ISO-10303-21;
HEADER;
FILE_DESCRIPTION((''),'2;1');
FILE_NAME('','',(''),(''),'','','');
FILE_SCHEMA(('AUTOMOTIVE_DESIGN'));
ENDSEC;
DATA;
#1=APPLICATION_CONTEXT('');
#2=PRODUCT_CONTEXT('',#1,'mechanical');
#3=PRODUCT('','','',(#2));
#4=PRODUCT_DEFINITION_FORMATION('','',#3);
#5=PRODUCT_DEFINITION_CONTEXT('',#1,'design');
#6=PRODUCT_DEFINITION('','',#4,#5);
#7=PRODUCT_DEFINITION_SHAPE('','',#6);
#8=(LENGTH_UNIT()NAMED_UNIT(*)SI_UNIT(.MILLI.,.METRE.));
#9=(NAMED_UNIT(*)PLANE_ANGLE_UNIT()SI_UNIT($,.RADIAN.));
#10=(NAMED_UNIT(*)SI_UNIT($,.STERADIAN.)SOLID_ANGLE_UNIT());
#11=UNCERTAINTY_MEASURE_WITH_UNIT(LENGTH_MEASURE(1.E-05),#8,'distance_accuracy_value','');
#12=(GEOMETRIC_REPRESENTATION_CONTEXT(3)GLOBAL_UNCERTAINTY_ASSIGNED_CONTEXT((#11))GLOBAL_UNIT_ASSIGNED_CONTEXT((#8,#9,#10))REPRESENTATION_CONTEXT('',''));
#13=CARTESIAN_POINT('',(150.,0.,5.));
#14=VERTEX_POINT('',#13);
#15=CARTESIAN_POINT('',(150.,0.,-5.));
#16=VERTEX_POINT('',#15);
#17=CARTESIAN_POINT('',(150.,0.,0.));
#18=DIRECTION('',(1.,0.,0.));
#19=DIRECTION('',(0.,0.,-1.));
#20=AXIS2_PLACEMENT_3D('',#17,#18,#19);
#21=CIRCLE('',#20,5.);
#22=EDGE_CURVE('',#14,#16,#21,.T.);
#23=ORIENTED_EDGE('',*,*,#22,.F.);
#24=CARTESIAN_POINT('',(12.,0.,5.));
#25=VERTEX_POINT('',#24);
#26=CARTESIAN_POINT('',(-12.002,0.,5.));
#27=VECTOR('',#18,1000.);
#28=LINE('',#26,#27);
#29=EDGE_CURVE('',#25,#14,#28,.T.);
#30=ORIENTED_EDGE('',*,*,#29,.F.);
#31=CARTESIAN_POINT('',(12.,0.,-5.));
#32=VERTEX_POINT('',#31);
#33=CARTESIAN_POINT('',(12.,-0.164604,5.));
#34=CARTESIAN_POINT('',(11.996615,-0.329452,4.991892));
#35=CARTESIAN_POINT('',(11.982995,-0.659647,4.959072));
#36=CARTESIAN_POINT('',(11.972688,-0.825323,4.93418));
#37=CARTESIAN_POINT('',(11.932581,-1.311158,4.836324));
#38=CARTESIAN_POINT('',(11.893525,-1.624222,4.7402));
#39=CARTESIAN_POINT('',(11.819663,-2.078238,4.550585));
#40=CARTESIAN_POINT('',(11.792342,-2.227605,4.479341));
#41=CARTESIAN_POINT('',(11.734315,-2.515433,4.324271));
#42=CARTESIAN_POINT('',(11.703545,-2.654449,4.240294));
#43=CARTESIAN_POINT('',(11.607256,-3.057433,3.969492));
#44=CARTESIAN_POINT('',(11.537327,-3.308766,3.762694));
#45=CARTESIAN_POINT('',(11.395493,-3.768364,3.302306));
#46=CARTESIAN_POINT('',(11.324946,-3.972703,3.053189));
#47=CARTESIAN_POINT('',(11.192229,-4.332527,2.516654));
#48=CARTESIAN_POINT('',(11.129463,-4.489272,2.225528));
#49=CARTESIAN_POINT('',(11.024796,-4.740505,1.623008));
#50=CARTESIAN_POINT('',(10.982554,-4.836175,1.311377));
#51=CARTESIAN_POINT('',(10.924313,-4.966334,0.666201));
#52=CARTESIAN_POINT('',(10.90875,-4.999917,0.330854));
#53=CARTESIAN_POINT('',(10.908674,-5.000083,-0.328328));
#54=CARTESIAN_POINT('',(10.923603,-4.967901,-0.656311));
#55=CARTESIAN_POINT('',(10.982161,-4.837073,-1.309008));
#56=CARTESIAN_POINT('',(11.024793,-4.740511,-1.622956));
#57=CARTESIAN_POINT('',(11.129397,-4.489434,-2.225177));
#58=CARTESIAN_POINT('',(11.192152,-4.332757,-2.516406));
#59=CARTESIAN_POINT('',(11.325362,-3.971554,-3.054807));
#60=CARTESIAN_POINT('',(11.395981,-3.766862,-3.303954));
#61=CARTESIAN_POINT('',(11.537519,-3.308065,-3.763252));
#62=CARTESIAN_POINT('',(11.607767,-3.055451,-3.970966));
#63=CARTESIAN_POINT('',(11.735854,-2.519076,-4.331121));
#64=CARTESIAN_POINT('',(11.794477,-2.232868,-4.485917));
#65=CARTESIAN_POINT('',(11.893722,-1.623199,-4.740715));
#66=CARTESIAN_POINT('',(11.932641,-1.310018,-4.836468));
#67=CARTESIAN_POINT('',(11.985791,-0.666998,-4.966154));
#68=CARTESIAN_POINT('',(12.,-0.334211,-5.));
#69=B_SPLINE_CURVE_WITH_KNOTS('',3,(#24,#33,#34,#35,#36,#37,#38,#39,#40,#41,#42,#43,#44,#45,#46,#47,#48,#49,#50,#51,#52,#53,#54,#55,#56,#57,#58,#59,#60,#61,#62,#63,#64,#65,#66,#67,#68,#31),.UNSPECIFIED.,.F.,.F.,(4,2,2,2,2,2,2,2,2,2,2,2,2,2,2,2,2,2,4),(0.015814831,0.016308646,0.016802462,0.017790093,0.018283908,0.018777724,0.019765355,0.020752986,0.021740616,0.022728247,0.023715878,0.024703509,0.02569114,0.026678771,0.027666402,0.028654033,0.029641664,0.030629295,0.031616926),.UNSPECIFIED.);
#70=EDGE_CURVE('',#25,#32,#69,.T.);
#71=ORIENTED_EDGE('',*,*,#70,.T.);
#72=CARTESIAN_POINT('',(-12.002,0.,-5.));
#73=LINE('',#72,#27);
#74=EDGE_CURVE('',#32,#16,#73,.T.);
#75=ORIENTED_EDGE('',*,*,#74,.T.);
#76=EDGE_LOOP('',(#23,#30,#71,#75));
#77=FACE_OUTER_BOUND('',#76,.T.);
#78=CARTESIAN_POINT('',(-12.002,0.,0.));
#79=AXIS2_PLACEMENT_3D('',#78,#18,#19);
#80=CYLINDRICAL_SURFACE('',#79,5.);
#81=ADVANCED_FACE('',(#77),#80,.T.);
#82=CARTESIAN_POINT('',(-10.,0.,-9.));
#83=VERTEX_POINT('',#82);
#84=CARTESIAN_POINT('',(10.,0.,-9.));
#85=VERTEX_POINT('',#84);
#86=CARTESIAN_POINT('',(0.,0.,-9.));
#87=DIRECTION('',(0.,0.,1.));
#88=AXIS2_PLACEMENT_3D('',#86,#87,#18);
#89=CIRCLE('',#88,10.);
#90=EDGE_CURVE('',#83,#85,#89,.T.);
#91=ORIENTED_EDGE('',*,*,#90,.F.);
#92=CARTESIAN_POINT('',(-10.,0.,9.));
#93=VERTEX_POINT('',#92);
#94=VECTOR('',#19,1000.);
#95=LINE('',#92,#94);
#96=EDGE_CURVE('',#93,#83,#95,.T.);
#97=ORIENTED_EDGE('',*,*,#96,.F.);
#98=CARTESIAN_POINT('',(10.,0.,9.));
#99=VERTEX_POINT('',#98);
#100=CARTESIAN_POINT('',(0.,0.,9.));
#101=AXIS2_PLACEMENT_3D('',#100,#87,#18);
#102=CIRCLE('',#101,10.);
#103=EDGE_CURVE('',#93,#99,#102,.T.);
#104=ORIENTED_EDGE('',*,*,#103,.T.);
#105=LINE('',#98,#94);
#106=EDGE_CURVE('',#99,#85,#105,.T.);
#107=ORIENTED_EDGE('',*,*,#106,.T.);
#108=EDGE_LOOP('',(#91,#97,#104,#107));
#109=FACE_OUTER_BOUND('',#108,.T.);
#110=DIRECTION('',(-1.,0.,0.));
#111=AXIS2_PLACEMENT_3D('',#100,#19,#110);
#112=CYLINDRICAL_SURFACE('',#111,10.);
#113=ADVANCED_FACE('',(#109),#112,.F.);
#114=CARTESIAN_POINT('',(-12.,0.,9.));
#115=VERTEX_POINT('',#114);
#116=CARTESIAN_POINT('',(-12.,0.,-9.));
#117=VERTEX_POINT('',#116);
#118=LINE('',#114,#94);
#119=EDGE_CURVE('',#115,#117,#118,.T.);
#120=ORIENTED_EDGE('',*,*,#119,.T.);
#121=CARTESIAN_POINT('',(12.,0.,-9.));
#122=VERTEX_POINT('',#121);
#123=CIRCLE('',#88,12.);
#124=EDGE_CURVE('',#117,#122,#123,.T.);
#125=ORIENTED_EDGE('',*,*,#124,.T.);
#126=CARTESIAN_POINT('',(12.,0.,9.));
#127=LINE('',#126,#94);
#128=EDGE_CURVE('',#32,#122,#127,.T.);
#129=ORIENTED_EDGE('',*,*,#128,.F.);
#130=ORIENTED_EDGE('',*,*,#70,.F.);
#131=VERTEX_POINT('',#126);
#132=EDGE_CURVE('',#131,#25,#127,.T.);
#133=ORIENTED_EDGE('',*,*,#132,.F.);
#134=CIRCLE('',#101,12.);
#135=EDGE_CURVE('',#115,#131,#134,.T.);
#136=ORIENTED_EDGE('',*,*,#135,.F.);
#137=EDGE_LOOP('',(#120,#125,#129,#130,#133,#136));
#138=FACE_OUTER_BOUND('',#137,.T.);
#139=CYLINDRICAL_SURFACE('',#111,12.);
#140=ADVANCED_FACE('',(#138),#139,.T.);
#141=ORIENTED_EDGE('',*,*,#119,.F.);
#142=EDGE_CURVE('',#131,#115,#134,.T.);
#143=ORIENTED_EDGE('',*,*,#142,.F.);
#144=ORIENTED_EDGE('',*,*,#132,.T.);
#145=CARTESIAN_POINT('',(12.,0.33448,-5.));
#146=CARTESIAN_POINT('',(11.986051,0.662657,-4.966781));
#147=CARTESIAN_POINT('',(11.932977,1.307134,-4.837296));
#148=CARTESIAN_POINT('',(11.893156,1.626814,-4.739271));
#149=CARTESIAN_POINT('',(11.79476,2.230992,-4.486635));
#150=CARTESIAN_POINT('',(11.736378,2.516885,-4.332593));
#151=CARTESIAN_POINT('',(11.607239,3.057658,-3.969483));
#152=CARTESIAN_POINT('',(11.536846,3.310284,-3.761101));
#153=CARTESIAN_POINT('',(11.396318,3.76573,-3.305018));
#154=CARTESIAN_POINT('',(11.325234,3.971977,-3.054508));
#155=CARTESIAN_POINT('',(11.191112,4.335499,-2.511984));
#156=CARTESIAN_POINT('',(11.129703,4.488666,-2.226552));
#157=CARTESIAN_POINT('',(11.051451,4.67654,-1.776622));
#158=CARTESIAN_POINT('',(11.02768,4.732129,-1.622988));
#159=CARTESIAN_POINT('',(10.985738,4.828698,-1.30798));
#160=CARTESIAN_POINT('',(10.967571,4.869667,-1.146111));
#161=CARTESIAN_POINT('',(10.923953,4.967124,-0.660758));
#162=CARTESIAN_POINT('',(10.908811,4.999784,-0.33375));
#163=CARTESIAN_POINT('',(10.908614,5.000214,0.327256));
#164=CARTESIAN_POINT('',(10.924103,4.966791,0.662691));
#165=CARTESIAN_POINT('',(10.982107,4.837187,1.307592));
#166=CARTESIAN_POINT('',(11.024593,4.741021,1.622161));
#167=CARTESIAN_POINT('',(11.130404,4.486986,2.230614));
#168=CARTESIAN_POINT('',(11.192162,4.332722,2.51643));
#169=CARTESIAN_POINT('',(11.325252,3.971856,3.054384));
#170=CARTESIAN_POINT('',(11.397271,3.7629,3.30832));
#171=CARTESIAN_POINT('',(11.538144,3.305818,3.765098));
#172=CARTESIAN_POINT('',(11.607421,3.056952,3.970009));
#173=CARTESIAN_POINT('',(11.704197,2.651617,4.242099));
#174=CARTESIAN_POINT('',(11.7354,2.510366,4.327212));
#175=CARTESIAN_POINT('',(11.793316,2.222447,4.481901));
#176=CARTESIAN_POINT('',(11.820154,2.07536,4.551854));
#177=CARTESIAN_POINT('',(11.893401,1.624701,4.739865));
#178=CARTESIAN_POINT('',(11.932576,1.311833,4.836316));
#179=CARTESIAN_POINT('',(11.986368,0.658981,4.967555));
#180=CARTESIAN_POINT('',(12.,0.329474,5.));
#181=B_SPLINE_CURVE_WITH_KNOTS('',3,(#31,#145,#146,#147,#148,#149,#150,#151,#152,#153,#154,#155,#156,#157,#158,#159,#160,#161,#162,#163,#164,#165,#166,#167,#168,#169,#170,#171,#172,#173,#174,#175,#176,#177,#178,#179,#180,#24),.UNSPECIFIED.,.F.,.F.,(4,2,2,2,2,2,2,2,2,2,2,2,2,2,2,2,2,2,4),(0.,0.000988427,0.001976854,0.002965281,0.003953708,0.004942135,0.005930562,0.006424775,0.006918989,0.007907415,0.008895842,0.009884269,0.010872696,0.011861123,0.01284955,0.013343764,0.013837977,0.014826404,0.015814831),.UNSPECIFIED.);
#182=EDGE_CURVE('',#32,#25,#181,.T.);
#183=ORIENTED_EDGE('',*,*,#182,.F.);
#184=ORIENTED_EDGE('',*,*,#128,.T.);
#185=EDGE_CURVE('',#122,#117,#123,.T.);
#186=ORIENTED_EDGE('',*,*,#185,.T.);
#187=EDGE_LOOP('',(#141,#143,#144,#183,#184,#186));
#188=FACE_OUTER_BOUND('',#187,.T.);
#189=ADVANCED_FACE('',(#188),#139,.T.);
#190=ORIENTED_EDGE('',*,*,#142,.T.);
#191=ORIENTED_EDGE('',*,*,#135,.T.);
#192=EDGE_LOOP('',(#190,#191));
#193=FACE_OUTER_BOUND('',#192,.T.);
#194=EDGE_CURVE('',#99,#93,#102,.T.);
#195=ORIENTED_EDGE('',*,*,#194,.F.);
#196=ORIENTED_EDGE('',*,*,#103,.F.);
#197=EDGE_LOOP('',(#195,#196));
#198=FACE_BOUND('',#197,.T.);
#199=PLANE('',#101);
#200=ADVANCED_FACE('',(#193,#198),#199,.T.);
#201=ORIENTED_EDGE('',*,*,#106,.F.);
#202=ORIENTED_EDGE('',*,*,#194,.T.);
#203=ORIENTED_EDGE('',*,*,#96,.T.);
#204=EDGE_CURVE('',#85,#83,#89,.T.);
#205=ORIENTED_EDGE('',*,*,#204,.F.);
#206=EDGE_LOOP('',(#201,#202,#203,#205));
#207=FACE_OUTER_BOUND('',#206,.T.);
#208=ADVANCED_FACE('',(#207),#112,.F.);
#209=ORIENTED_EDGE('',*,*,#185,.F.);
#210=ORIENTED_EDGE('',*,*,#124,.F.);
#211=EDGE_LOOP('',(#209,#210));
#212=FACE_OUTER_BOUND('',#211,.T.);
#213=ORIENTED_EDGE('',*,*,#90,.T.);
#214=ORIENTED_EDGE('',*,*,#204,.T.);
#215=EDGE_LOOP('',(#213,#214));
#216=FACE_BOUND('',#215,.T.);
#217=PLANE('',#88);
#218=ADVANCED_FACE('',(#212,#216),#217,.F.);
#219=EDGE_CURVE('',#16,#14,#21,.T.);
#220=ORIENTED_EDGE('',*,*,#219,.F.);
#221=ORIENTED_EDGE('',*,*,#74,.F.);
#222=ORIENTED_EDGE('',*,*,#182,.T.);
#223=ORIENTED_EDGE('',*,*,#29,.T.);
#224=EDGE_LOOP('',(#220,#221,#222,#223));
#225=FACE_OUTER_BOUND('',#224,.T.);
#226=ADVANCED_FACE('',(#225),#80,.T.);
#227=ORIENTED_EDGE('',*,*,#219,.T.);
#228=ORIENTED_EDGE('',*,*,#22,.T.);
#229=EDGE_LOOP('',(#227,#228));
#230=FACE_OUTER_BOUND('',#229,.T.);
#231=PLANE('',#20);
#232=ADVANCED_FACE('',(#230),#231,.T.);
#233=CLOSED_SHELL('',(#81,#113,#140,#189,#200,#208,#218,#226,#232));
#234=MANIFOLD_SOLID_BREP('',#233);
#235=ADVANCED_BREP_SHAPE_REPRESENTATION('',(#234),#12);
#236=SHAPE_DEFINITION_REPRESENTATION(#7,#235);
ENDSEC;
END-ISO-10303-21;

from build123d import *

# Parameters (mm, degrees)
SKETCH1_R                = 12
SKETCH1_R_2              = 10
BOSS_EXTRUDE1_DEPTH      = 9
BOSS_EXTRUDE2_REACH      = 164.693
BOSS_EXTRUDE2_END_RADIUS = 12
SKETCH2_R                = 5


with BuildPart() as part:
    # Sketch1 → Boss-Extrude1 (new, symmetric)
    with BuildSketch(Plane.XY):
        Circle(SKETCH1_R)
        Circle(SKETCH1_R_2, mode=Mode.SUBTRACT)
    extrude(amount=BOSS_EXTRUDE1_DEPTH, both=True)

    # Boss-Extrude2: up to this cylinder (the profile starts outside it)
    boss_extrude2_end = Plane(origin=(0, 0, 0), z_dir=(0, 0, -1)) * Cylinder(BOSS_EXTRUDE2_END_RADIUS, 354.386, mode=Mode.PRIVATE)
    # Sketch2 → Boss-Extrude2 (add, up to the surface)
    with BuildSketch(Plane(origin=(150, 0, 0), x_dir=(0, 0, -1), z_dir=(1, 0, 0)), mode=Mode.PRIVATE) as boss_extrude2_sk1:
        Circle(SKETCH2_R)
    boss_extrude2_tool1 = extrude(boss_extrude2_sk1.sketch, amount=-BOSS_EXTRUDE2_REACH, mode=Mode.PRIVATE) - boss_extrude2_end
    add(boss_extrude2_tool1.solids().sort_by_distance((150, 0, 0))[0])


solid = part.part
